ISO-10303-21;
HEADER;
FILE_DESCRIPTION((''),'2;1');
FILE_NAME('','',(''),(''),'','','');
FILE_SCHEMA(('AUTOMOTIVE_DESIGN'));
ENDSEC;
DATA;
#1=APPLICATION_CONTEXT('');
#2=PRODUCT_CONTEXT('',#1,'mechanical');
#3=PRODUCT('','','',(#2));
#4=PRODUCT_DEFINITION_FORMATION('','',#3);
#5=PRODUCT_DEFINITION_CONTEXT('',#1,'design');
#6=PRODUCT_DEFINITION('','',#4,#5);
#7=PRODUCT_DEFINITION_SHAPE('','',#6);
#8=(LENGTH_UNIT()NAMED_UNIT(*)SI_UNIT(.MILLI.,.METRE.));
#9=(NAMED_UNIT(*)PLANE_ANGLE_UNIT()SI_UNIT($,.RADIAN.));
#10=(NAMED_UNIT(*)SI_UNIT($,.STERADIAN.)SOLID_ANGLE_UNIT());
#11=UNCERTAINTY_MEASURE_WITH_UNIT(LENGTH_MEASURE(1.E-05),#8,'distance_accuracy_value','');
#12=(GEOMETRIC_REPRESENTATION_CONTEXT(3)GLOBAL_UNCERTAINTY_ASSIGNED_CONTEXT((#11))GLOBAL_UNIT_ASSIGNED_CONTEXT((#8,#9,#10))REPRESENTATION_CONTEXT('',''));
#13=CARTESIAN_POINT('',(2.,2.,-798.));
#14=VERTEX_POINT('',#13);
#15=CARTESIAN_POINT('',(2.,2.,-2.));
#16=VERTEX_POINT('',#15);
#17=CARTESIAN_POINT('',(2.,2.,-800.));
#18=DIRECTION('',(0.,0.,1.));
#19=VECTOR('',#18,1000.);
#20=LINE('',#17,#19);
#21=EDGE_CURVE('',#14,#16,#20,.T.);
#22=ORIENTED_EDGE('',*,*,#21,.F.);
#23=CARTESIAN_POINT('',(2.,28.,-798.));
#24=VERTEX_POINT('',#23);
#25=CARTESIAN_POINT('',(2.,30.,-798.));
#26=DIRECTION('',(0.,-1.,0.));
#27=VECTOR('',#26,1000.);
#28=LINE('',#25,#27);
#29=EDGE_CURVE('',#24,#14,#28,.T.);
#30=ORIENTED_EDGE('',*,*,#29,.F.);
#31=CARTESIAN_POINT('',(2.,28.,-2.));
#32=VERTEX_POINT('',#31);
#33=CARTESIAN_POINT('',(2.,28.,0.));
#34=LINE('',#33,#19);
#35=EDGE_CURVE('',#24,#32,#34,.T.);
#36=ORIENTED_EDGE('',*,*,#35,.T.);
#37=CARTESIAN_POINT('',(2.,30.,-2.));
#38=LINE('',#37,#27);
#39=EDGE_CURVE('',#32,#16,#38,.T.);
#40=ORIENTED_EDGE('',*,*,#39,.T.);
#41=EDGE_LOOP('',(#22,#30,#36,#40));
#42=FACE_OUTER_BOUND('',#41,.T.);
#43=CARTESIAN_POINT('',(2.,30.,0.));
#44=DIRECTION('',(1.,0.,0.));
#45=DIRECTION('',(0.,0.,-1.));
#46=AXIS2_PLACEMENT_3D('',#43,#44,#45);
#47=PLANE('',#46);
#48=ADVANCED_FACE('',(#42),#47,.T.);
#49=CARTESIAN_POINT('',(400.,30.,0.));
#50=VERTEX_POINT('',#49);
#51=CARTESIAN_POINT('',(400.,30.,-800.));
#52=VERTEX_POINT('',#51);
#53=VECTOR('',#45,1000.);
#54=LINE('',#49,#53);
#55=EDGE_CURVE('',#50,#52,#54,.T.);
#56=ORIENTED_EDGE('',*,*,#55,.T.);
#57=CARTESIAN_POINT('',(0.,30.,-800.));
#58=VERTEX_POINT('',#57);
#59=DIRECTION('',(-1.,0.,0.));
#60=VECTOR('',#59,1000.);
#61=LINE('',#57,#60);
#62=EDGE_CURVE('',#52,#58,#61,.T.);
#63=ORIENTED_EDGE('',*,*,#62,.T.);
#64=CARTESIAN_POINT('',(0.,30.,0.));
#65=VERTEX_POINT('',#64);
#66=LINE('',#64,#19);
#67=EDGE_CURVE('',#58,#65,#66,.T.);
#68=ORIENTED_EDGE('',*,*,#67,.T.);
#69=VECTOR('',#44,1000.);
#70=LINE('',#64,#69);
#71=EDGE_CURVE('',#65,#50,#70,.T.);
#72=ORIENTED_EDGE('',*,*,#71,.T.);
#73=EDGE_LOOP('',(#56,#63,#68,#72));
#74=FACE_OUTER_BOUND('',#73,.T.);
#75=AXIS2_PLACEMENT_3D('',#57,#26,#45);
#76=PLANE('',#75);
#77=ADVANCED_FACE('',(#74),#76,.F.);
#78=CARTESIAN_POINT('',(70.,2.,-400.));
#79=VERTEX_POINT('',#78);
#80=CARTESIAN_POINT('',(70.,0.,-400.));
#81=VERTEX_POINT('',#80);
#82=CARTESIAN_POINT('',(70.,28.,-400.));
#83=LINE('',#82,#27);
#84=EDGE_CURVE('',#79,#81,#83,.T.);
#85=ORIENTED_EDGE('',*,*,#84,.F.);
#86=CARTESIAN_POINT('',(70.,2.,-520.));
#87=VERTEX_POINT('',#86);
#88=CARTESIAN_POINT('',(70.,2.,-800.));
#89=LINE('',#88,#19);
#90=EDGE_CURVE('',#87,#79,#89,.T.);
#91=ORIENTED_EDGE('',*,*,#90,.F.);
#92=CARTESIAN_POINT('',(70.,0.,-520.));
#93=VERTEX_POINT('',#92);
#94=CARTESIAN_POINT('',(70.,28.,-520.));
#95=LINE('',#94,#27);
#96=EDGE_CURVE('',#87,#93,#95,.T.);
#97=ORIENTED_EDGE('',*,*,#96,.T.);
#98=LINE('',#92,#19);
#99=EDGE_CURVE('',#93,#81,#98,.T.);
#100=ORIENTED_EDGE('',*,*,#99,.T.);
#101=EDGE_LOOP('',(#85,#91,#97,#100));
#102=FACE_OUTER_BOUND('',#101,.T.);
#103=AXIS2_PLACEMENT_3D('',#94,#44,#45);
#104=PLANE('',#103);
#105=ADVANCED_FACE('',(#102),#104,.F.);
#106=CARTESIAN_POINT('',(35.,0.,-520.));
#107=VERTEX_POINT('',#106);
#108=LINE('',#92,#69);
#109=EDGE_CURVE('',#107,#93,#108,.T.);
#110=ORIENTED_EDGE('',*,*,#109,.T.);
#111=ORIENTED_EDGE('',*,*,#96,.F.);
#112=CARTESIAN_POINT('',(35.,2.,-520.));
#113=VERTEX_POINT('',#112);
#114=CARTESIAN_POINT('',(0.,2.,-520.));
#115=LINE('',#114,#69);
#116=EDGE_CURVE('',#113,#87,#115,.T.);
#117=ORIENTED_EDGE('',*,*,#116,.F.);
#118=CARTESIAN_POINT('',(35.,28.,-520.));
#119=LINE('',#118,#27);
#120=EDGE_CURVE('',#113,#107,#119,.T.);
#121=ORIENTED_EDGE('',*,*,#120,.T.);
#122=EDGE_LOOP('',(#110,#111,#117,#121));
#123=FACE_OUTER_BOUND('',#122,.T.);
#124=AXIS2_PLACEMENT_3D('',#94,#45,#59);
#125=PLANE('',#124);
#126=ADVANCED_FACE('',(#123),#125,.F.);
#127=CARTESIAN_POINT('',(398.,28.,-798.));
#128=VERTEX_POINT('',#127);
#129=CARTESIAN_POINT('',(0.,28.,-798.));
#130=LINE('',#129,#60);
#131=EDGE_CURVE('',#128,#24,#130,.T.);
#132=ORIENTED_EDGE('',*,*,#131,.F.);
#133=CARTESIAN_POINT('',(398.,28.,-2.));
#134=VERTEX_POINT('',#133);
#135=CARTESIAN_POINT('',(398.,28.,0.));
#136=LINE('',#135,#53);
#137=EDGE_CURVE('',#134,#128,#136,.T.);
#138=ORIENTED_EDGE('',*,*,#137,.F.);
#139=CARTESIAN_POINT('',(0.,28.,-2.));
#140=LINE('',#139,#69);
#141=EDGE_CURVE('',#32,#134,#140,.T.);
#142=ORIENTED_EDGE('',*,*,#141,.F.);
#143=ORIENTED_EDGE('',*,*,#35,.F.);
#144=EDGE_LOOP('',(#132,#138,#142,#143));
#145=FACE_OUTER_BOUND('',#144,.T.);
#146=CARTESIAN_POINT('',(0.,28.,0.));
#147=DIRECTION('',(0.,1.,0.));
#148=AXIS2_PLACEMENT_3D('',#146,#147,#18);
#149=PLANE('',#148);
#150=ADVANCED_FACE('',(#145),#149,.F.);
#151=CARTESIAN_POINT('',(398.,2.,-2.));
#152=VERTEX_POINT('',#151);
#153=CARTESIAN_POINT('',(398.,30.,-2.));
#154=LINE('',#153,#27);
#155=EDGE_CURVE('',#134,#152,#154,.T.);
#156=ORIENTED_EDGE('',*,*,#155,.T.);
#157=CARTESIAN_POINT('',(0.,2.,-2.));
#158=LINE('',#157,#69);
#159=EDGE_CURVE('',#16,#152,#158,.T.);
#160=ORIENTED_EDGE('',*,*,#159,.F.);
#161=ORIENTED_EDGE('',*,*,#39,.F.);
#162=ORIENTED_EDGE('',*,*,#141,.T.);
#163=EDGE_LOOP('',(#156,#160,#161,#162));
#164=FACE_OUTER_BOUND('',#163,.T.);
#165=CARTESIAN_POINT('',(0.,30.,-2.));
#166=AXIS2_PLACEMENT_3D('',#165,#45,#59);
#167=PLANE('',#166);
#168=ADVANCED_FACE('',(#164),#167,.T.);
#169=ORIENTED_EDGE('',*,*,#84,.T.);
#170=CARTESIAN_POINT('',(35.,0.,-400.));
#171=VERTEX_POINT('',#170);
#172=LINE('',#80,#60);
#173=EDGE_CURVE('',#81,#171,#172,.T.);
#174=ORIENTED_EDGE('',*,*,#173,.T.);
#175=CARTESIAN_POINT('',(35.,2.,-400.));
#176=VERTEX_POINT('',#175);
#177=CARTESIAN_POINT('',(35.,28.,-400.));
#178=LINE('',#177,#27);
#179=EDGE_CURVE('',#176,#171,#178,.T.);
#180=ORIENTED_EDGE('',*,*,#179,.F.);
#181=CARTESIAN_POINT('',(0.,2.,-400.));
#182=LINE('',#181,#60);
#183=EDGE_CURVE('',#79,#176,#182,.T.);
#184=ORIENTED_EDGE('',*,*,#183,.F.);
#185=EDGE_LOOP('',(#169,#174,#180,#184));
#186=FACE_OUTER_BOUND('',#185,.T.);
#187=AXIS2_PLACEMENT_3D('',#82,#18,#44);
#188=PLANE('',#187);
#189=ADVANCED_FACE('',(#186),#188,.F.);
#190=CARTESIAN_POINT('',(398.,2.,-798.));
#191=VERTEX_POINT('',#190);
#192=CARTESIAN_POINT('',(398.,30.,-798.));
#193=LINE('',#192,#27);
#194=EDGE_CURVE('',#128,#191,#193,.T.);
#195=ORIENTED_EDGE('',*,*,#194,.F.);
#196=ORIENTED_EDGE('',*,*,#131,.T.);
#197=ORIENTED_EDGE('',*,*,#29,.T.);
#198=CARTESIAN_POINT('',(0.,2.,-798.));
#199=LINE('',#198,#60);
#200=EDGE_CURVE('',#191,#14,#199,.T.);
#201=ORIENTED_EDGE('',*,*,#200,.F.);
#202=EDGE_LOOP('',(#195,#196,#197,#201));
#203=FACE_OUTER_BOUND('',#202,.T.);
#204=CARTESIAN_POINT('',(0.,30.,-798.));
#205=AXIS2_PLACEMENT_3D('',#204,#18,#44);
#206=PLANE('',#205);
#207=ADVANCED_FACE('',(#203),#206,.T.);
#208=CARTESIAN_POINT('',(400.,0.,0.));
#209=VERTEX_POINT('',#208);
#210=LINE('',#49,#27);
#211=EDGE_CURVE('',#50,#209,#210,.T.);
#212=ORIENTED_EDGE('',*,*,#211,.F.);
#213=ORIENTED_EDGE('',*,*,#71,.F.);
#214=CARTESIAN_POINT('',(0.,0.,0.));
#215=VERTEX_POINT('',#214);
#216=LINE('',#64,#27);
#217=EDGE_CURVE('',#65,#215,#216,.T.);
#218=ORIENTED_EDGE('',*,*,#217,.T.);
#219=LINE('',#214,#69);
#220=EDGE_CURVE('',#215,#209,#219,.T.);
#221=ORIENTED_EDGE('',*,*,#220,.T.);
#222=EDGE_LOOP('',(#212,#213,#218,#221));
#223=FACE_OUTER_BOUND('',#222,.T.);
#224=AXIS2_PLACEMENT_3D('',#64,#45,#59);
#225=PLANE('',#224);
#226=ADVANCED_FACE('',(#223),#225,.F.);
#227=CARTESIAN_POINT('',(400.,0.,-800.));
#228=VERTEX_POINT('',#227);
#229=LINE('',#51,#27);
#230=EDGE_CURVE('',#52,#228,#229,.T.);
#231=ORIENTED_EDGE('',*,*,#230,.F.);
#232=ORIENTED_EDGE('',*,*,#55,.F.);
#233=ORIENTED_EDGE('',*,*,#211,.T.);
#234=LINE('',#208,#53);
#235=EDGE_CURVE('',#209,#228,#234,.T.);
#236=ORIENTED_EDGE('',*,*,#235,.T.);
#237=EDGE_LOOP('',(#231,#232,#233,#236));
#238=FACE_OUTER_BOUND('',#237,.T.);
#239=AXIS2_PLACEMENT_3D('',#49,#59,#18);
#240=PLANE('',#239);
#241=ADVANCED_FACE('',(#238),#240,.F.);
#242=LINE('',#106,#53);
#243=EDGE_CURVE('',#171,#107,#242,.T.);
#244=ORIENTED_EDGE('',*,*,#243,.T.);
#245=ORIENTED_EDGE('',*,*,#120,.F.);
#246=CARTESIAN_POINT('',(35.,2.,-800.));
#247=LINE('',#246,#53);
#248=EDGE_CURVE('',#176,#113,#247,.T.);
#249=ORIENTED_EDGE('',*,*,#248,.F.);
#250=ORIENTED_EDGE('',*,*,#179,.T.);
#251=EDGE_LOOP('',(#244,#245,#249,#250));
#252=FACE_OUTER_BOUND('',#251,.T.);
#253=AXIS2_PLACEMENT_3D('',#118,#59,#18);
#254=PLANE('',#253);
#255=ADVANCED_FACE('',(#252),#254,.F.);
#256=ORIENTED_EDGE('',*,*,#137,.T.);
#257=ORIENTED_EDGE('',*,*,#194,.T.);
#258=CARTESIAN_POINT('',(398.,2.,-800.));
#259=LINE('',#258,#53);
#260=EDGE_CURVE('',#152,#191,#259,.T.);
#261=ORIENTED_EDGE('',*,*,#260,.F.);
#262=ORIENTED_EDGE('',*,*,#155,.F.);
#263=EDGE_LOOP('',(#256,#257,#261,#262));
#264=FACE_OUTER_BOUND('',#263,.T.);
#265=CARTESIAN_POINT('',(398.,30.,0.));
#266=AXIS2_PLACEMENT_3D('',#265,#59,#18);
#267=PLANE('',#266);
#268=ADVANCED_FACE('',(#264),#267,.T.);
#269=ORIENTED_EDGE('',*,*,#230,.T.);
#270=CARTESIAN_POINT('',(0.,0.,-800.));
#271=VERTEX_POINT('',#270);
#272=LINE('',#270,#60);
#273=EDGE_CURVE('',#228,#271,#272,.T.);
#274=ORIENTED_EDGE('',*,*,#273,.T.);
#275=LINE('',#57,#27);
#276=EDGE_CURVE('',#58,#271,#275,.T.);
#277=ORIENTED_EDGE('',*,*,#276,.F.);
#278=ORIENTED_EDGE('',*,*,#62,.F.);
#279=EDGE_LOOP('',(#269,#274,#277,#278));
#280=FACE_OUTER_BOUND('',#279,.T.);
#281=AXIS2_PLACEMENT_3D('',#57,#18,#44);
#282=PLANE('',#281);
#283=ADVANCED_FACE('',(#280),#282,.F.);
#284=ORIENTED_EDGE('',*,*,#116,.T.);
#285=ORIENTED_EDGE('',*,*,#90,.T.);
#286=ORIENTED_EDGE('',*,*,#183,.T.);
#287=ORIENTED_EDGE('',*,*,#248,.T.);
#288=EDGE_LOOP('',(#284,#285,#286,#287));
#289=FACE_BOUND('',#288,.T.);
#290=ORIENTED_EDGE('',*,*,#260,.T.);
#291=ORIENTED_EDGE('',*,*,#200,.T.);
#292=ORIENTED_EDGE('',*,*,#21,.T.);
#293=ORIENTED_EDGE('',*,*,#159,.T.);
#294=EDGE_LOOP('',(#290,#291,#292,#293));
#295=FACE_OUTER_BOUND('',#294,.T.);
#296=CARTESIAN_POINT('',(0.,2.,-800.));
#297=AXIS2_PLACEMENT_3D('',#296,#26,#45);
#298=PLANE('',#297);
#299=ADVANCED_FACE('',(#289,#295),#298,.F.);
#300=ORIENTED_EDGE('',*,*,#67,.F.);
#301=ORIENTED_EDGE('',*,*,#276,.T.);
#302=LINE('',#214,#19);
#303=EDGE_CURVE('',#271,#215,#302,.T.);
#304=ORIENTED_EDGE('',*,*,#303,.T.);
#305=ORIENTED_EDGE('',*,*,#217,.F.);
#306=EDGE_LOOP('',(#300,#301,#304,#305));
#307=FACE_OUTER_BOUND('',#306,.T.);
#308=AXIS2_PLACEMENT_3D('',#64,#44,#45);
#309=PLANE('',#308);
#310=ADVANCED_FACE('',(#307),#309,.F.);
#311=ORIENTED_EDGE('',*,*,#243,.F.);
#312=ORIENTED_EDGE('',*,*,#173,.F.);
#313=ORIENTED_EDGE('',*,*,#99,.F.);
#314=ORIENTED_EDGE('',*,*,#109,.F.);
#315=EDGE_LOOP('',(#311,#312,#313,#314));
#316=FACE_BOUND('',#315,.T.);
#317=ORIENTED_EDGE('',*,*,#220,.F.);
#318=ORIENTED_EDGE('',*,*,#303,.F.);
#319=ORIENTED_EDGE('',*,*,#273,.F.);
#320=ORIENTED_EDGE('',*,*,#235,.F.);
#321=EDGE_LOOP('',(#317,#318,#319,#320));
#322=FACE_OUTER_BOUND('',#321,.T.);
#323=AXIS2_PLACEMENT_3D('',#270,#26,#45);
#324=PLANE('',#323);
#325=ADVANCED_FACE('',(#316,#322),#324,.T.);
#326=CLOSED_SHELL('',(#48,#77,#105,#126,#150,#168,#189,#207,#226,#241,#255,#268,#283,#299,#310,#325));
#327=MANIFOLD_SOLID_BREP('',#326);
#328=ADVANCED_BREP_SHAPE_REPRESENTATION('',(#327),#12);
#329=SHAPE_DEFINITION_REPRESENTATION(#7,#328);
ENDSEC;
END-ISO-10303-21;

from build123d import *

# Parameters (mm, degrees)
SKETCH_1_W          = 400
SKETCH_1_H          = 800
EXTRUDE_1_DEPTH     = 30
SHELL_1_T           = -2
SKETCH_2_W          = 35
SKETCH_2_H          = 120
CUT_EXTRUDE_1_DEPTH = 28
SKETCH_3_W          = 400
SKETCH_3_H          = 800
EXTRUDE_2_DEPTH     = 2


with BuildPart() as part:
    # 草图1 → 凸台-拉伸1 (new body)
    with BuildSketch(Plane(origin=(0, 0, 0), x_dir=(1, 0, 0), z_dir=(0, 1, 0))):
        with Locations((200, 400)):
            Rectangle(SKETCH_1_W, SKETCH_1_H)
    extrude(amount=EXTRUDE_1_DEPTH)

    # 抽壳1
    shell_1_openings = [part.faces().sort_by_distance(p)[0] for p in [
        (200, 30, -400),
    ]]
    offset(amount=SHELL_1_T, openings=shell_1_openings, kind=Kind.INTERSECTION)

    # 草图2 → 切除-拉伸1 (cut)
    with BuildSketch(Plane.XZ):
        with Locations((52.5, -460)):
            Rectangle(SKETCH_2_W, SKETCH_2_H)
    extrude(amount=-CUT_EXTRUDE_1_DEPTH, mode=Mode.SUBTRACT)

    # 草图3 → 凸台-拉伸2 (add)
    with BuildSketch(Plane(origin=(0, 30, 0), x_dir=(1, 0, 0), z_dir=(0, 1, 0))):
        with Locations((200, 400)):
            Rectangle(SKETCH_3_W, SKETCH_3_H)
    extrude(amount=-EXTRUDE_2_DEPTH)


solid = part.part
